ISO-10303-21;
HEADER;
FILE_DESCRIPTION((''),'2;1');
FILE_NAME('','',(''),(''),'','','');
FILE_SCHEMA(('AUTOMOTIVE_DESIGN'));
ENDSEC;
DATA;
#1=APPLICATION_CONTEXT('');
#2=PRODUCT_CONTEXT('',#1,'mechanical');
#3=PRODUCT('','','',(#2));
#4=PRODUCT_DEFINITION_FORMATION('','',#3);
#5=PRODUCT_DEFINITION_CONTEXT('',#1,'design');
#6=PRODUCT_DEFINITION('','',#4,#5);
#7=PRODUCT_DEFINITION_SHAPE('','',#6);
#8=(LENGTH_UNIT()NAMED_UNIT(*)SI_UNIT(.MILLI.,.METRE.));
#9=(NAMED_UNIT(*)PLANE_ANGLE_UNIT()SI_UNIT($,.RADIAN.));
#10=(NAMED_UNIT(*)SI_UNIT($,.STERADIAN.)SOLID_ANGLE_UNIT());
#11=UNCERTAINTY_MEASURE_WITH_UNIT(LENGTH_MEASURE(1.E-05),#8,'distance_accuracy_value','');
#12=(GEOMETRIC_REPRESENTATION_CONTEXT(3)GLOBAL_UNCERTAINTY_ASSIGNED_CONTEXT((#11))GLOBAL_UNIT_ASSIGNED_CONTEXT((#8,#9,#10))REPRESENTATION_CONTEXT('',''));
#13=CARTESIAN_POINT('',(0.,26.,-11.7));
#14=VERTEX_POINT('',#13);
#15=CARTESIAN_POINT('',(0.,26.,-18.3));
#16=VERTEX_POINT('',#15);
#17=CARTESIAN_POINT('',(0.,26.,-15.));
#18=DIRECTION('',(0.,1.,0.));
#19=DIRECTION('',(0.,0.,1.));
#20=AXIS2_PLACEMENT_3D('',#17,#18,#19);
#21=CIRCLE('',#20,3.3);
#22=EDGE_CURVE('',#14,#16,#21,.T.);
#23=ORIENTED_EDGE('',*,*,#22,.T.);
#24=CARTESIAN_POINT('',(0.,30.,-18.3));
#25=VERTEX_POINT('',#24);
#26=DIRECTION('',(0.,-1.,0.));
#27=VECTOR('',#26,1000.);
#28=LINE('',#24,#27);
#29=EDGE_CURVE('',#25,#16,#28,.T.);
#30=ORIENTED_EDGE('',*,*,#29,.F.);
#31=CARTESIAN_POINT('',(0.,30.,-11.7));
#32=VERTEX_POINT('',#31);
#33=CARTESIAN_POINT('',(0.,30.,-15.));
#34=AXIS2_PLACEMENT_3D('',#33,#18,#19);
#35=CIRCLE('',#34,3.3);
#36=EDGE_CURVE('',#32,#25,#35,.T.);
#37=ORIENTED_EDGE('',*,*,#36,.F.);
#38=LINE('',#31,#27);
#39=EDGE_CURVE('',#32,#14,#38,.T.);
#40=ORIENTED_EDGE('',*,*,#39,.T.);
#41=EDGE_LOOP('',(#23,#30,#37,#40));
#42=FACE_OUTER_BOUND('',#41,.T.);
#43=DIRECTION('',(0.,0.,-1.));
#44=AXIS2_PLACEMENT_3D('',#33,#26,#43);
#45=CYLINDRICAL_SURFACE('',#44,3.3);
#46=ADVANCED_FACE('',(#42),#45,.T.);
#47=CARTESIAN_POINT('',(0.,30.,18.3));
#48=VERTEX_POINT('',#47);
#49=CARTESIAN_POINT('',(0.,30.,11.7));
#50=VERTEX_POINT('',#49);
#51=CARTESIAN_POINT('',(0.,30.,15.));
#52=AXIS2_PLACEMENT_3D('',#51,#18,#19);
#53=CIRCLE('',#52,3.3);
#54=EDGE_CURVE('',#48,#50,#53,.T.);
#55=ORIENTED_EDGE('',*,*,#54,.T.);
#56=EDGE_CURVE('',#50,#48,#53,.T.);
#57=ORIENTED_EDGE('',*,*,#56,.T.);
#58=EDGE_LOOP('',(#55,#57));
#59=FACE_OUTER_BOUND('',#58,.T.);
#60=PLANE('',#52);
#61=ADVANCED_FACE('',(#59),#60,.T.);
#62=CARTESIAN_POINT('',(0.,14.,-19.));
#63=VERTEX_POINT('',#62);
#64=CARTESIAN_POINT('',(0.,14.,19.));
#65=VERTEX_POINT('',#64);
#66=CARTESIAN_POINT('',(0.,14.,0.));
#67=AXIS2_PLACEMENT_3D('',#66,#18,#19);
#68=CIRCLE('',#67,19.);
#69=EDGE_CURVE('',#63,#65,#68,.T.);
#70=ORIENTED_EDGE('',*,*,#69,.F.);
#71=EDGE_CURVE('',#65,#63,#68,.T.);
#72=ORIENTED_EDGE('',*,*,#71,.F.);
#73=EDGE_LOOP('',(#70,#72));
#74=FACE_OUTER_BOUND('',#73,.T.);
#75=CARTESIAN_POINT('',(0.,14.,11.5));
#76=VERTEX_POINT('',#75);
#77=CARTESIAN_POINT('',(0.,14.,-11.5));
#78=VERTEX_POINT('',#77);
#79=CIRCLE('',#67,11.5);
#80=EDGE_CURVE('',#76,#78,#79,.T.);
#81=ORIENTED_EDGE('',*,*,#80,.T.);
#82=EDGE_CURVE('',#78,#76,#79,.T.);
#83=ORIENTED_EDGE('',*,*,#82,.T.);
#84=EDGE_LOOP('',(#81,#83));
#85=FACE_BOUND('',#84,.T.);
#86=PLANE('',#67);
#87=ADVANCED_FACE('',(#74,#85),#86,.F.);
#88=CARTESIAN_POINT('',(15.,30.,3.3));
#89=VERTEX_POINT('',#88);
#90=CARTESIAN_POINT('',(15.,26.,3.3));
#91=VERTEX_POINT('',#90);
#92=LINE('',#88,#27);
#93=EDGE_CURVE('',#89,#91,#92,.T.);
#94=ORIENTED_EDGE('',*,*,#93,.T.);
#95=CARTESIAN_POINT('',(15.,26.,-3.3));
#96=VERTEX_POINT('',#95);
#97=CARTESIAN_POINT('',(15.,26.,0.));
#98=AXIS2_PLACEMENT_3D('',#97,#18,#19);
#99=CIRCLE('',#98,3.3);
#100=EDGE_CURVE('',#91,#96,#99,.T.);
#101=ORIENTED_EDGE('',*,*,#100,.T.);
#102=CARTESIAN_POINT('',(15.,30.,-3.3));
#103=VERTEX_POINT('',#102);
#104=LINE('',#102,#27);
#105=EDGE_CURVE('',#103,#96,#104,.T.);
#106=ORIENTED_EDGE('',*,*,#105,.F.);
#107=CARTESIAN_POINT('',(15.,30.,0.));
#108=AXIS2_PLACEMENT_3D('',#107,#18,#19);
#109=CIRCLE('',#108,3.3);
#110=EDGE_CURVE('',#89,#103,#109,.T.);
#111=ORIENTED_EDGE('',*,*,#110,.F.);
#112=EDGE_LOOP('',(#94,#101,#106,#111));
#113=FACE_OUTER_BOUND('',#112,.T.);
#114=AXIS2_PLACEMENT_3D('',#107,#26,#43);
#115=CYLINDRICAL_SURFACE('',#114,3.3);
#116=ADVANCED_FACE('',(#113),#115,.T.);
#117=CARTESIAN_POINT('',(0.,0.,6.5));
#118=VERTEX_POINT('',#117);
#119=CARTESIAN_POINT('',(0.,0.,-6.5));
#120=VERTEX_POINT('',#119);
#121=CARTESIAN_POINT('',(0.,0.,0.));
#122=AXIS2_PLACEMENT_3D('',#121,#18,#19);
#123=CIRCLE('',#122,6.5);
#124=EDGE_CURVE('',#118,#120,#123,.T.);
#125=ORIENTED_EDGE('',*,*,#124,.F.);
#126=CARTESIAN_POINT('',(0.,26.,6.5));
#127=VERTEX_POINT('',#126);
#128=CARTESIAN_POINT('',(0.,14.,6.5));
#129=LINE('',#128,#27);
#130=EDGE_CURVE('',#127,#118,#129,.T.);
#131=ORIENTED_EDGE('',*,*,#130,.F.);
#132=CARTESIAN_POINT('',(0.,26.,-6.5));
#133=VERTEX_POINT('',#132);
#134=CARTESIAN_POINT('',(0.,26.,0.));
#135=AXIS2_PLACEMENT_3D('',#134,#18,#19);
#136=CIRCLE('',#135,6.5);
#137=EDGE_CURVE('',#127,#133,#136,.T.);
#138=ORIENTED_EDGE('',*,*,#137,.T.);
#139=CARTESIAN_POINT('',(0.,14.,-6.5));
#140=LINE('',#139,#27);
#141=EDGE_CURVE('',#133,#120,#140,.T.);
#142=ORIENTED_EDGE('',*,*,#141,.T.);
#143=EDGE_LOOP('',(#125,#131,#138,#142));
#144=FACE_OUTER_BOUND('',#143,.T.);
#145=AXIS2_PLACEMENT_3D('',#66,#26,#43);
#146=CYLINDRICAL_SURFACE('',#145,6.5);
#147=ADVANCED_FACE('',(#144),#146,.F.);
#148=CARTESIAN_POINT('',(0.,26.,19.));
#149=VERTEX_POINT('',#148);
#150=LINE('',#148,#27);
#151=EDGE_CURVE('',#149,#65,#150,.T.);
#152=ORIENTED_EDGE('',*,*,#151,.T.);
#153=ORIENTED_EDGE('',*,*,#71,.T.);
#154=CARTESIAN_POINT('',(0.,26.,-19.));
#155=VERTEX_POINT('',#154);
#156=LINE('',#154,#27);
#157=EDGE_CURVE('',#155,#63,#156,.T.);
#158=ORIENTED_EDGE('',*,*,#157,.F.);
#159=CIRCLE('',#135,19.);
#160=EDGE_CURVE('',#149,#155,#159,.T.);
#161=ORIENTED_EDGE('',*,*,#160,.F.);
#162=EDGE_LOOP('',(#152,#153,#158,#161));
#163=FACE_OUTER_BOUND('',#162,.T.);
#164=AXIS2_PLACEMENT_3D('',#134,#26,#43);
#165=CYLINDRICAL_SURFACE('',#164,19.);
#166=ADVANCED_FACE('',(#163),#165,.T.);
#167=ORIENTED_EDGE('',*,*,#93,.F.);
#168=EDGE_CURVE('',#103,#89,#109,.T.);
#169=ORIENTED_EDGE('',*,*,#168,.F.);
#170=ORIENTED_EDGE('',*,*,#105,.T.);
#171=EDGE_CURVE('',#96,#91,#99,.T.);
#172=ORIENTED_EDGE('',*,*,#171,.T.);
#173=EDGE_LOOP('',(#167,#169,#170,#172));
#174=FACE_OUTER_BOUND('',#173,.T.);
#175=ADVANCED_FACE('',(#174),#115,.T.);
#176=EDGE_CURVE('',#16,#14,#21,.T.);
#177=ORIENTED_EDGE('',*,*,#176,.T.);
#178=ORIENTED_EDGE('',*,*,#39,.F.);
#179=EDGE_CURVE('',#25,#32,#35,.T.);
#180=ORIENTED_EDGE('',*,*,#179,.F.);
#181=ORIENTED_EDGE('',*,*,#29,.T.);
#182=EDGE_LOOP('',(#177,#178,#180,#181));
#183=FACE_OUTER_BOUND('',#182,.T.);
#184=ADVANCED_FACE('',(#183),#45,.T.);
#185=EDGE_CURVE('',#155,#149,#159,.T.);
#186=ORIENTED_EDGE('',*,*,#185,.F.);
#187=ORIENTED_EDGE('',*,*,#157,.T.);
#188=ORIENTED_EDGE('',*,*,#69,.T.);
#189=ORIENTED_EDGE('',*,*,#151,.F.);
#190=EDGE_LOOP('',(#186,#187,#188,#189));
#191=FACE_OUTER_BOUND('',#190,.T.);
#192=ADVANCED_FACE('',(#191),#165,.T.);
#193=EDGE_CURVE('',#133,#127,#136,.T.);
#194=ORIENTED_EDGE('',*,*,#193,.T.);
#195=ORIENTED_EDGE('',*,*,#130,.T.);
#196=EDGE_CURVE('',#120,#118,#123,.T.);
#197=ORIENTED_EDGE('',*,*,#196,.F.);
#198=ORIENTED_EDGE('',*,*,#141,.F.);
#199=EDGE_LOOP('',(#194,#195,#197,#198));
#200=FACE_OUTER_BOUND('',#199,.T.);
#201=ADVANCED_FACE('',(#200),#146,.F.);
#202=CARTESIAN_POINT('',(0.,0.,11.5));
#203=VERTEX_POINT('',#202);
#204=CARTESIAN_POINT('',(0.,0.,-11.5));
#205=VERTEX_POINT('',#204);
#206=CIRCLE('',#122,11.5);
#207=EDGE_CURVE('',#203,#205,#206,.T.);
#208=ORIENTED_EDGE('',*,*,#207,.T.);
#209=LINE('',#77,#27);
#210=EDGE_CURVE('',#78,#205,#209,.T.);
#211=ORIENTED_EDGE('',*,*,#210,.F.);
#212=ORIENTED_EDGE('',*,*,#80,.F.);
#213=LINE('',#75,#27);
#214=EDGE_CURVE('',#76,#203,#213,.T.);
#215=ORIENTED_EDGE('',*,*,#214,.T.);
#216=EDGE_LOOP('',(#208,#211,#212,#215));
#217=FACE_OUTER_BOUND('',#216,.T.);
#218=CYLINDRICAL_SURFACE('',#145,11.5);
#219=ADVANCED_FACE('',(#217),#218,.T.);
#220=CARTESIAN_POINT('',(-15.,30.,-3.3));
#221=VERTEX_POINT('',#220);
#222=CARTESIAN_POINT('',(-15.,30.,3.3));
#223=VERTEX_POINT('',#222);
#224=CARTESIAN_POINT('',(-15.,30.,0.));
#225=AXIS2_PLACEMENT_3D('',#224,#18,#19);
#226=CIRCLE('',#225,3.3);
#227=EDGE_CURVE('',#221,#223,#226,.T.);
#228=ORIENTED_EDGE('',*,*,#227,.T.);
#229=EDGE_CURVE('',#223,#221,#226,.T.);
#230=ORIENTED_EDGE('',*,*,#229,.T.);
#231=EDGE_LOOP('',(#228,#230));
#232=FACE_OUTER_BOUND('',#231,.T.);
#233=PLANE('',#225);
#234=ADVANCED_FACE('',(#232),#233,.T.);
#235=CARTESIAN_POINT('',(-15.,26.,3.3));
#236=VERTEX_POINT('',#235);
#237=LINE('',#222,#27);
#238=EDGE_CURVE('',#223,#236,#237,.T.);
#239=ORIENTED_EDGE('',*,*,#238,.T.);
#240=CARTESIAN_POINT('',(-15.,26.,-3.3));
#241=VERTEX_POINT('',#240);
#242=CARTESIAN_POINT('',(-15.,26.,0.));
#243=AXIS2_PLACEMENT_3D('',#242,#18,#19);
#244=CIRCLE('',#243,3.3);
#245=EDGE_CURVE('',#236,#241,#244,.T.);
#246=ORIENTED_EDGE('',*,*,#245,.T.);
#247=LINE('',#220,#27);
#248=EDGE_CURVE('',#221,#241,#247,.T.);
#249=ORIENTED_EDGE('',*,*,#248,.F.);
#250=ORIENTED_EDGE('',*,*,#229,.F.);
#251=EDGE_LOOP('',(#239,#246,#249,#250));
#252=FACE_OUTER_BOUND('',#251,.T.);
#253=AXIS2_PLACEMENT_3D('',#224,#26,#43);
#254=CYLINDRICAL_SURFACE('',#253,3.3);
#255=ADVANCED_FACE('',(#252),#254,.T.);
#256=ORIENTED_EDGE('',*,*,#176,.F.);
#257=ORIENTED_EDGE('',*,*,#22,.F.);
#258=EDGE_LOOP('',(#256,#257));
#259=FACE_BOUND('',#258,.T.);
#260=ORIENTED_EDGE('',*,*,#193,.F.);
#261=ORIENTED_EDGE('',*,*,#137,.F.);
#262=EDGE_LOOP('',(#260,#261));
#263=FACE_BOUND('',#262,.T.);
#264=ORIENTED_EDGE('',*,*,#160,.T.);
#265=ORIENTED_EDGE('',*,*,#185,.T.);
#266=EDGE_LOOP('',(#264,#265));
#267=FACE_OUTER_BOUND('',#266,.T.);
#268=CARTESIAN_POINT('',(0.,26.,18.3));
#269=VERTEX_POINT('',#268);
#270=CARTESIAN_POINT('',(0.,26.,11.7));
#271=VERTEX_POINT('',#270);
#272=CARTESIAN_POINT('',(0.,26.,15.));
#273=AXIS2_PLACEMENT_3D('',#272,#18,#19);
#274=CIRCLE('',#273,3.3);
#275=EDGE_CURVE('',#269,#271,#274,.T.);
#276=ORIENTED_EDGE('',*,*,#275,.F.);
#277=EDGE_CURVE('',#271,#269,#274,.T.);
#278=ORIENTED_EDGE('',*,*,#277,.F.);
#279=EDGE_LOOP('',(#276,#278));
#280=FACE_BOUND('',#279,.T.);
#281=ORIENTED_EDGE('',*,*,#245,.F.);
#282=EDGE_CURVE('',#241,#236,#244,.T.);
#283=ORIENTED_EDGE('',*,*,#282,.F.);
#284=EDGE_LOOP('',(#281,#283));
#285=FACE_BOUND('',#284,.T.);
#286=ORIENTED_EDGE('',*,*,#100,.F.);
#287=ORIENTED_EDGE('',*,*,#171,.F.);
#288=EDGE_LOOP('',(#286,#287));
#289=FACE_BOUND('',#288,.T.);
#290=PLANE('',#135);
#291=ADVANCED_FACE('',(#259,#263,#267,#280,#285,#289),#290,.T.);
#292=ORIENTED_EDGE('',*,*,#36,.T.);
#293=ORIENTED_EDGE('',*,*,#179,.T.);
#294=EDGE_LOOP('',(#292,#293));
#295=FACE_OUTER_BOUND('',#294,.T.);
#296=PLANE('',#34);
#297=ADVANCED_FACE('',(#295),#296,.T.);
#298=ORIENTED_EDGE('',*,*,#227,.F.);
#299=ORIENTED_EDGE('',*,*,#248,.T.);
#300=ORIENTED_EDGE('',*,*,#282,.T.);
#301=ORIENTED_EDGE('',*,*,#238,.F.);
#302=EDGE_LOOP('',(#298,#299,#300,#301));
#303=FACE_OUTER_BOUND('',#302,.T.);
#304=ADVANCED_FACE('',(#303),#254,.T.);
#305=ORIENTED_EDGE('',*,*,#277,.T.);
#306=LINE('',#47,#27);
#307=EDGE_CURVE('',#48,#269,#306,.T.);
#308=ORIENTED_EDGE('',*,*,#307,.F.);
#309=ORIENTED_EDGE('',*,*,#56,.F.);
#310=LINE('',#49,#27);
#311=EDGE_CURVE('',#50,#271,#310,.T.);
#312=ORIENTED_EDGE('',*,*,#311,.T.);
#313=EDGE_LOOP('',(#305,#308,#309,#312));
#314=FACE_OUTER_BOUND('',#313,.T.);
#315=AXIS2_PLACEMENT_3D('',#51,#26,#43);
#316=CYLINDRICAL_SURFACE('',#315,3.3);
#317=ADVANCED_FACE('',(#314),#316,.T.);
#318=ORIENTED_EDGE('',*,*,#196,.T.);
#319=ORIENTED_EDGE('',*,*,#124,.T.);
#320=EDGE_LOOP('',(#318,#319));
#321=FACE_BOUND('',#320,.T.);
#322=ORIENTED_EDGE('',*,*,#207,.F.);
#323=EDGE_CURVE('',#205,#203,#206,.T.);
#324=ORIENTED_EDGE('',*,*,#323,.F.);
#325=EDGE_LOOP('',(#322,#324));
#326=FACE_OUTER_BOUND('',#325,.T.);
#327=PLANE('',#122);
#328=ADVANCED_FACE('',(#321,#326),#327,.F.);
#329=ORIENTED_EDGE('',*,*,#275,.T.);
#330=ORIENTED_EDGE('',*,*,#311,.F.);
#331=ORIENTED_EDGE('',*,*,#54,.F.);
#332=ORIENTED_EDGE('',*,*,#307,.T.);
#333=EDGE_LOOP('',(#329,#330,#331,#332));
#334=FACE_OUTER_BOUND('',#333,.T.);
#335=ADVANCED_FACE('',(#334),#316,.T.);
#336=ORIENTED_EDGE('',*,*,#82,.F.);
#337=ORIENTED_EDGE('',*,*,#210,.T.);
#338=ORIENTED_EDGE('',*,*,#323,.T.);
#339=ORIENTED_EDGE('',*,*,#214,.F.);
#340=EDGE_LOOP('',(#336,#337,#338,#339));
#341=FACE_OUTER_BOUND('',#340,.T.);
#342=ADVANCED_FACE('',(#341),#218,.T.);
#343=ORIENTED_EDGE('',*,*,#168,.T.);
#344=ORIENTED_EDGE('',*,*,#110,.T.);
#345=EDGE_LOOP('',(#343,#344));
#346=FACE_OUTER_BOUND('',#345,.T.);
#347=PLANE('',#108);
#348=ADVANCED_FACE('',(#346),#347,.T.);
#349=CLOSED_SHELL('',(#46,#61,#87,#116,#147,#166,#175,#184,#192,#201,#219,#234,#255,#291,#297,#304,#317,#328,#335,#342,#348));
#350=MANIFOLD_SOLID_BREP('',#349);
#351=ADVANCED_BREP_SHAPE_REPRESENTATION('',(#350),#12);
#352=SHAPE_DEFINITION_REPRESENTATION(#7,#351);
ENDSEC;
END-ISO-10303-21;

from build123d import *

# Parameters (mm, degrees)
SKETCH_1_R      = 11.5
SKETCH_1_R_2    = 6.5
EXTRUDE_1_DEPTH = 14
SKETCH_2_R      = 19
SKETCH_2_R_2    = 6.5
EXTRUDE_2_DEPTH = 12
SKETCH_3_R      = 3.3
EXTRUDE_3_DEPTH = 4


with BuildPart() as part:
    # 草图1 → 拉伸1 (new body)
    with BuildSketch(Plane(origin=(0, 0, 0), x_dir=(1, 0, 0), z_dir=(0, 1, 0))):
        with Locations(Location((0, 0, 0), (0, 0, 270))):
            Circle(SKETCH_1_R)
        with Locations(Location((0, 0, 0), (0, 0, 270))):
            Circle(SKETCH_1_R_2, mode=Mode.SUBTRACT)
    extrude(amount=EXTRUDE_1_DEPTH)

    # 草图2 → 拉伸2 (add)
    with BuildSketch(Plane(origin=(0, 14, 0), x_dir=(-1, 0, 0), z_dir=(0, 1, 0))):
        with Locations(Location((0, 0, 0), (0, 0, 90))):
            Circle(SKETCH_2_R)
        with Locations(Location((0, 0, 0), (0, 0, 90))):
            Circle(SKETCH_2_R_2, mode=Mode.SUBTRACT)
    extrude(amount=EXTRUDE_2_DEPTH)

    # 草图3 → 拉伸3 (add)
    with BuildSketch(Plane(origin=(0, 26, 0), x_dir=(-1, 0, 0), z_dir=(0, 1, 0))):
        with Locations(Location((-15, 0, 0), (0, 0, 90))):
            Circle(SKETCH_3_R)
        with Locations(Location((0, -15, 0), (0, 0, 90))):
            Circle(SKETCH_3_R)
        with Locations(Location((0, 15, 0), (0, 0, 90))):
            Circle(SKETCH_3_R)
        with Locations(Location((15, 0, 0), (0, 0, 90))):
            Circle(SKETCH_3_R)
    extrude(amount=EXTRUDE_3_DEPTH)


solid = part.part
